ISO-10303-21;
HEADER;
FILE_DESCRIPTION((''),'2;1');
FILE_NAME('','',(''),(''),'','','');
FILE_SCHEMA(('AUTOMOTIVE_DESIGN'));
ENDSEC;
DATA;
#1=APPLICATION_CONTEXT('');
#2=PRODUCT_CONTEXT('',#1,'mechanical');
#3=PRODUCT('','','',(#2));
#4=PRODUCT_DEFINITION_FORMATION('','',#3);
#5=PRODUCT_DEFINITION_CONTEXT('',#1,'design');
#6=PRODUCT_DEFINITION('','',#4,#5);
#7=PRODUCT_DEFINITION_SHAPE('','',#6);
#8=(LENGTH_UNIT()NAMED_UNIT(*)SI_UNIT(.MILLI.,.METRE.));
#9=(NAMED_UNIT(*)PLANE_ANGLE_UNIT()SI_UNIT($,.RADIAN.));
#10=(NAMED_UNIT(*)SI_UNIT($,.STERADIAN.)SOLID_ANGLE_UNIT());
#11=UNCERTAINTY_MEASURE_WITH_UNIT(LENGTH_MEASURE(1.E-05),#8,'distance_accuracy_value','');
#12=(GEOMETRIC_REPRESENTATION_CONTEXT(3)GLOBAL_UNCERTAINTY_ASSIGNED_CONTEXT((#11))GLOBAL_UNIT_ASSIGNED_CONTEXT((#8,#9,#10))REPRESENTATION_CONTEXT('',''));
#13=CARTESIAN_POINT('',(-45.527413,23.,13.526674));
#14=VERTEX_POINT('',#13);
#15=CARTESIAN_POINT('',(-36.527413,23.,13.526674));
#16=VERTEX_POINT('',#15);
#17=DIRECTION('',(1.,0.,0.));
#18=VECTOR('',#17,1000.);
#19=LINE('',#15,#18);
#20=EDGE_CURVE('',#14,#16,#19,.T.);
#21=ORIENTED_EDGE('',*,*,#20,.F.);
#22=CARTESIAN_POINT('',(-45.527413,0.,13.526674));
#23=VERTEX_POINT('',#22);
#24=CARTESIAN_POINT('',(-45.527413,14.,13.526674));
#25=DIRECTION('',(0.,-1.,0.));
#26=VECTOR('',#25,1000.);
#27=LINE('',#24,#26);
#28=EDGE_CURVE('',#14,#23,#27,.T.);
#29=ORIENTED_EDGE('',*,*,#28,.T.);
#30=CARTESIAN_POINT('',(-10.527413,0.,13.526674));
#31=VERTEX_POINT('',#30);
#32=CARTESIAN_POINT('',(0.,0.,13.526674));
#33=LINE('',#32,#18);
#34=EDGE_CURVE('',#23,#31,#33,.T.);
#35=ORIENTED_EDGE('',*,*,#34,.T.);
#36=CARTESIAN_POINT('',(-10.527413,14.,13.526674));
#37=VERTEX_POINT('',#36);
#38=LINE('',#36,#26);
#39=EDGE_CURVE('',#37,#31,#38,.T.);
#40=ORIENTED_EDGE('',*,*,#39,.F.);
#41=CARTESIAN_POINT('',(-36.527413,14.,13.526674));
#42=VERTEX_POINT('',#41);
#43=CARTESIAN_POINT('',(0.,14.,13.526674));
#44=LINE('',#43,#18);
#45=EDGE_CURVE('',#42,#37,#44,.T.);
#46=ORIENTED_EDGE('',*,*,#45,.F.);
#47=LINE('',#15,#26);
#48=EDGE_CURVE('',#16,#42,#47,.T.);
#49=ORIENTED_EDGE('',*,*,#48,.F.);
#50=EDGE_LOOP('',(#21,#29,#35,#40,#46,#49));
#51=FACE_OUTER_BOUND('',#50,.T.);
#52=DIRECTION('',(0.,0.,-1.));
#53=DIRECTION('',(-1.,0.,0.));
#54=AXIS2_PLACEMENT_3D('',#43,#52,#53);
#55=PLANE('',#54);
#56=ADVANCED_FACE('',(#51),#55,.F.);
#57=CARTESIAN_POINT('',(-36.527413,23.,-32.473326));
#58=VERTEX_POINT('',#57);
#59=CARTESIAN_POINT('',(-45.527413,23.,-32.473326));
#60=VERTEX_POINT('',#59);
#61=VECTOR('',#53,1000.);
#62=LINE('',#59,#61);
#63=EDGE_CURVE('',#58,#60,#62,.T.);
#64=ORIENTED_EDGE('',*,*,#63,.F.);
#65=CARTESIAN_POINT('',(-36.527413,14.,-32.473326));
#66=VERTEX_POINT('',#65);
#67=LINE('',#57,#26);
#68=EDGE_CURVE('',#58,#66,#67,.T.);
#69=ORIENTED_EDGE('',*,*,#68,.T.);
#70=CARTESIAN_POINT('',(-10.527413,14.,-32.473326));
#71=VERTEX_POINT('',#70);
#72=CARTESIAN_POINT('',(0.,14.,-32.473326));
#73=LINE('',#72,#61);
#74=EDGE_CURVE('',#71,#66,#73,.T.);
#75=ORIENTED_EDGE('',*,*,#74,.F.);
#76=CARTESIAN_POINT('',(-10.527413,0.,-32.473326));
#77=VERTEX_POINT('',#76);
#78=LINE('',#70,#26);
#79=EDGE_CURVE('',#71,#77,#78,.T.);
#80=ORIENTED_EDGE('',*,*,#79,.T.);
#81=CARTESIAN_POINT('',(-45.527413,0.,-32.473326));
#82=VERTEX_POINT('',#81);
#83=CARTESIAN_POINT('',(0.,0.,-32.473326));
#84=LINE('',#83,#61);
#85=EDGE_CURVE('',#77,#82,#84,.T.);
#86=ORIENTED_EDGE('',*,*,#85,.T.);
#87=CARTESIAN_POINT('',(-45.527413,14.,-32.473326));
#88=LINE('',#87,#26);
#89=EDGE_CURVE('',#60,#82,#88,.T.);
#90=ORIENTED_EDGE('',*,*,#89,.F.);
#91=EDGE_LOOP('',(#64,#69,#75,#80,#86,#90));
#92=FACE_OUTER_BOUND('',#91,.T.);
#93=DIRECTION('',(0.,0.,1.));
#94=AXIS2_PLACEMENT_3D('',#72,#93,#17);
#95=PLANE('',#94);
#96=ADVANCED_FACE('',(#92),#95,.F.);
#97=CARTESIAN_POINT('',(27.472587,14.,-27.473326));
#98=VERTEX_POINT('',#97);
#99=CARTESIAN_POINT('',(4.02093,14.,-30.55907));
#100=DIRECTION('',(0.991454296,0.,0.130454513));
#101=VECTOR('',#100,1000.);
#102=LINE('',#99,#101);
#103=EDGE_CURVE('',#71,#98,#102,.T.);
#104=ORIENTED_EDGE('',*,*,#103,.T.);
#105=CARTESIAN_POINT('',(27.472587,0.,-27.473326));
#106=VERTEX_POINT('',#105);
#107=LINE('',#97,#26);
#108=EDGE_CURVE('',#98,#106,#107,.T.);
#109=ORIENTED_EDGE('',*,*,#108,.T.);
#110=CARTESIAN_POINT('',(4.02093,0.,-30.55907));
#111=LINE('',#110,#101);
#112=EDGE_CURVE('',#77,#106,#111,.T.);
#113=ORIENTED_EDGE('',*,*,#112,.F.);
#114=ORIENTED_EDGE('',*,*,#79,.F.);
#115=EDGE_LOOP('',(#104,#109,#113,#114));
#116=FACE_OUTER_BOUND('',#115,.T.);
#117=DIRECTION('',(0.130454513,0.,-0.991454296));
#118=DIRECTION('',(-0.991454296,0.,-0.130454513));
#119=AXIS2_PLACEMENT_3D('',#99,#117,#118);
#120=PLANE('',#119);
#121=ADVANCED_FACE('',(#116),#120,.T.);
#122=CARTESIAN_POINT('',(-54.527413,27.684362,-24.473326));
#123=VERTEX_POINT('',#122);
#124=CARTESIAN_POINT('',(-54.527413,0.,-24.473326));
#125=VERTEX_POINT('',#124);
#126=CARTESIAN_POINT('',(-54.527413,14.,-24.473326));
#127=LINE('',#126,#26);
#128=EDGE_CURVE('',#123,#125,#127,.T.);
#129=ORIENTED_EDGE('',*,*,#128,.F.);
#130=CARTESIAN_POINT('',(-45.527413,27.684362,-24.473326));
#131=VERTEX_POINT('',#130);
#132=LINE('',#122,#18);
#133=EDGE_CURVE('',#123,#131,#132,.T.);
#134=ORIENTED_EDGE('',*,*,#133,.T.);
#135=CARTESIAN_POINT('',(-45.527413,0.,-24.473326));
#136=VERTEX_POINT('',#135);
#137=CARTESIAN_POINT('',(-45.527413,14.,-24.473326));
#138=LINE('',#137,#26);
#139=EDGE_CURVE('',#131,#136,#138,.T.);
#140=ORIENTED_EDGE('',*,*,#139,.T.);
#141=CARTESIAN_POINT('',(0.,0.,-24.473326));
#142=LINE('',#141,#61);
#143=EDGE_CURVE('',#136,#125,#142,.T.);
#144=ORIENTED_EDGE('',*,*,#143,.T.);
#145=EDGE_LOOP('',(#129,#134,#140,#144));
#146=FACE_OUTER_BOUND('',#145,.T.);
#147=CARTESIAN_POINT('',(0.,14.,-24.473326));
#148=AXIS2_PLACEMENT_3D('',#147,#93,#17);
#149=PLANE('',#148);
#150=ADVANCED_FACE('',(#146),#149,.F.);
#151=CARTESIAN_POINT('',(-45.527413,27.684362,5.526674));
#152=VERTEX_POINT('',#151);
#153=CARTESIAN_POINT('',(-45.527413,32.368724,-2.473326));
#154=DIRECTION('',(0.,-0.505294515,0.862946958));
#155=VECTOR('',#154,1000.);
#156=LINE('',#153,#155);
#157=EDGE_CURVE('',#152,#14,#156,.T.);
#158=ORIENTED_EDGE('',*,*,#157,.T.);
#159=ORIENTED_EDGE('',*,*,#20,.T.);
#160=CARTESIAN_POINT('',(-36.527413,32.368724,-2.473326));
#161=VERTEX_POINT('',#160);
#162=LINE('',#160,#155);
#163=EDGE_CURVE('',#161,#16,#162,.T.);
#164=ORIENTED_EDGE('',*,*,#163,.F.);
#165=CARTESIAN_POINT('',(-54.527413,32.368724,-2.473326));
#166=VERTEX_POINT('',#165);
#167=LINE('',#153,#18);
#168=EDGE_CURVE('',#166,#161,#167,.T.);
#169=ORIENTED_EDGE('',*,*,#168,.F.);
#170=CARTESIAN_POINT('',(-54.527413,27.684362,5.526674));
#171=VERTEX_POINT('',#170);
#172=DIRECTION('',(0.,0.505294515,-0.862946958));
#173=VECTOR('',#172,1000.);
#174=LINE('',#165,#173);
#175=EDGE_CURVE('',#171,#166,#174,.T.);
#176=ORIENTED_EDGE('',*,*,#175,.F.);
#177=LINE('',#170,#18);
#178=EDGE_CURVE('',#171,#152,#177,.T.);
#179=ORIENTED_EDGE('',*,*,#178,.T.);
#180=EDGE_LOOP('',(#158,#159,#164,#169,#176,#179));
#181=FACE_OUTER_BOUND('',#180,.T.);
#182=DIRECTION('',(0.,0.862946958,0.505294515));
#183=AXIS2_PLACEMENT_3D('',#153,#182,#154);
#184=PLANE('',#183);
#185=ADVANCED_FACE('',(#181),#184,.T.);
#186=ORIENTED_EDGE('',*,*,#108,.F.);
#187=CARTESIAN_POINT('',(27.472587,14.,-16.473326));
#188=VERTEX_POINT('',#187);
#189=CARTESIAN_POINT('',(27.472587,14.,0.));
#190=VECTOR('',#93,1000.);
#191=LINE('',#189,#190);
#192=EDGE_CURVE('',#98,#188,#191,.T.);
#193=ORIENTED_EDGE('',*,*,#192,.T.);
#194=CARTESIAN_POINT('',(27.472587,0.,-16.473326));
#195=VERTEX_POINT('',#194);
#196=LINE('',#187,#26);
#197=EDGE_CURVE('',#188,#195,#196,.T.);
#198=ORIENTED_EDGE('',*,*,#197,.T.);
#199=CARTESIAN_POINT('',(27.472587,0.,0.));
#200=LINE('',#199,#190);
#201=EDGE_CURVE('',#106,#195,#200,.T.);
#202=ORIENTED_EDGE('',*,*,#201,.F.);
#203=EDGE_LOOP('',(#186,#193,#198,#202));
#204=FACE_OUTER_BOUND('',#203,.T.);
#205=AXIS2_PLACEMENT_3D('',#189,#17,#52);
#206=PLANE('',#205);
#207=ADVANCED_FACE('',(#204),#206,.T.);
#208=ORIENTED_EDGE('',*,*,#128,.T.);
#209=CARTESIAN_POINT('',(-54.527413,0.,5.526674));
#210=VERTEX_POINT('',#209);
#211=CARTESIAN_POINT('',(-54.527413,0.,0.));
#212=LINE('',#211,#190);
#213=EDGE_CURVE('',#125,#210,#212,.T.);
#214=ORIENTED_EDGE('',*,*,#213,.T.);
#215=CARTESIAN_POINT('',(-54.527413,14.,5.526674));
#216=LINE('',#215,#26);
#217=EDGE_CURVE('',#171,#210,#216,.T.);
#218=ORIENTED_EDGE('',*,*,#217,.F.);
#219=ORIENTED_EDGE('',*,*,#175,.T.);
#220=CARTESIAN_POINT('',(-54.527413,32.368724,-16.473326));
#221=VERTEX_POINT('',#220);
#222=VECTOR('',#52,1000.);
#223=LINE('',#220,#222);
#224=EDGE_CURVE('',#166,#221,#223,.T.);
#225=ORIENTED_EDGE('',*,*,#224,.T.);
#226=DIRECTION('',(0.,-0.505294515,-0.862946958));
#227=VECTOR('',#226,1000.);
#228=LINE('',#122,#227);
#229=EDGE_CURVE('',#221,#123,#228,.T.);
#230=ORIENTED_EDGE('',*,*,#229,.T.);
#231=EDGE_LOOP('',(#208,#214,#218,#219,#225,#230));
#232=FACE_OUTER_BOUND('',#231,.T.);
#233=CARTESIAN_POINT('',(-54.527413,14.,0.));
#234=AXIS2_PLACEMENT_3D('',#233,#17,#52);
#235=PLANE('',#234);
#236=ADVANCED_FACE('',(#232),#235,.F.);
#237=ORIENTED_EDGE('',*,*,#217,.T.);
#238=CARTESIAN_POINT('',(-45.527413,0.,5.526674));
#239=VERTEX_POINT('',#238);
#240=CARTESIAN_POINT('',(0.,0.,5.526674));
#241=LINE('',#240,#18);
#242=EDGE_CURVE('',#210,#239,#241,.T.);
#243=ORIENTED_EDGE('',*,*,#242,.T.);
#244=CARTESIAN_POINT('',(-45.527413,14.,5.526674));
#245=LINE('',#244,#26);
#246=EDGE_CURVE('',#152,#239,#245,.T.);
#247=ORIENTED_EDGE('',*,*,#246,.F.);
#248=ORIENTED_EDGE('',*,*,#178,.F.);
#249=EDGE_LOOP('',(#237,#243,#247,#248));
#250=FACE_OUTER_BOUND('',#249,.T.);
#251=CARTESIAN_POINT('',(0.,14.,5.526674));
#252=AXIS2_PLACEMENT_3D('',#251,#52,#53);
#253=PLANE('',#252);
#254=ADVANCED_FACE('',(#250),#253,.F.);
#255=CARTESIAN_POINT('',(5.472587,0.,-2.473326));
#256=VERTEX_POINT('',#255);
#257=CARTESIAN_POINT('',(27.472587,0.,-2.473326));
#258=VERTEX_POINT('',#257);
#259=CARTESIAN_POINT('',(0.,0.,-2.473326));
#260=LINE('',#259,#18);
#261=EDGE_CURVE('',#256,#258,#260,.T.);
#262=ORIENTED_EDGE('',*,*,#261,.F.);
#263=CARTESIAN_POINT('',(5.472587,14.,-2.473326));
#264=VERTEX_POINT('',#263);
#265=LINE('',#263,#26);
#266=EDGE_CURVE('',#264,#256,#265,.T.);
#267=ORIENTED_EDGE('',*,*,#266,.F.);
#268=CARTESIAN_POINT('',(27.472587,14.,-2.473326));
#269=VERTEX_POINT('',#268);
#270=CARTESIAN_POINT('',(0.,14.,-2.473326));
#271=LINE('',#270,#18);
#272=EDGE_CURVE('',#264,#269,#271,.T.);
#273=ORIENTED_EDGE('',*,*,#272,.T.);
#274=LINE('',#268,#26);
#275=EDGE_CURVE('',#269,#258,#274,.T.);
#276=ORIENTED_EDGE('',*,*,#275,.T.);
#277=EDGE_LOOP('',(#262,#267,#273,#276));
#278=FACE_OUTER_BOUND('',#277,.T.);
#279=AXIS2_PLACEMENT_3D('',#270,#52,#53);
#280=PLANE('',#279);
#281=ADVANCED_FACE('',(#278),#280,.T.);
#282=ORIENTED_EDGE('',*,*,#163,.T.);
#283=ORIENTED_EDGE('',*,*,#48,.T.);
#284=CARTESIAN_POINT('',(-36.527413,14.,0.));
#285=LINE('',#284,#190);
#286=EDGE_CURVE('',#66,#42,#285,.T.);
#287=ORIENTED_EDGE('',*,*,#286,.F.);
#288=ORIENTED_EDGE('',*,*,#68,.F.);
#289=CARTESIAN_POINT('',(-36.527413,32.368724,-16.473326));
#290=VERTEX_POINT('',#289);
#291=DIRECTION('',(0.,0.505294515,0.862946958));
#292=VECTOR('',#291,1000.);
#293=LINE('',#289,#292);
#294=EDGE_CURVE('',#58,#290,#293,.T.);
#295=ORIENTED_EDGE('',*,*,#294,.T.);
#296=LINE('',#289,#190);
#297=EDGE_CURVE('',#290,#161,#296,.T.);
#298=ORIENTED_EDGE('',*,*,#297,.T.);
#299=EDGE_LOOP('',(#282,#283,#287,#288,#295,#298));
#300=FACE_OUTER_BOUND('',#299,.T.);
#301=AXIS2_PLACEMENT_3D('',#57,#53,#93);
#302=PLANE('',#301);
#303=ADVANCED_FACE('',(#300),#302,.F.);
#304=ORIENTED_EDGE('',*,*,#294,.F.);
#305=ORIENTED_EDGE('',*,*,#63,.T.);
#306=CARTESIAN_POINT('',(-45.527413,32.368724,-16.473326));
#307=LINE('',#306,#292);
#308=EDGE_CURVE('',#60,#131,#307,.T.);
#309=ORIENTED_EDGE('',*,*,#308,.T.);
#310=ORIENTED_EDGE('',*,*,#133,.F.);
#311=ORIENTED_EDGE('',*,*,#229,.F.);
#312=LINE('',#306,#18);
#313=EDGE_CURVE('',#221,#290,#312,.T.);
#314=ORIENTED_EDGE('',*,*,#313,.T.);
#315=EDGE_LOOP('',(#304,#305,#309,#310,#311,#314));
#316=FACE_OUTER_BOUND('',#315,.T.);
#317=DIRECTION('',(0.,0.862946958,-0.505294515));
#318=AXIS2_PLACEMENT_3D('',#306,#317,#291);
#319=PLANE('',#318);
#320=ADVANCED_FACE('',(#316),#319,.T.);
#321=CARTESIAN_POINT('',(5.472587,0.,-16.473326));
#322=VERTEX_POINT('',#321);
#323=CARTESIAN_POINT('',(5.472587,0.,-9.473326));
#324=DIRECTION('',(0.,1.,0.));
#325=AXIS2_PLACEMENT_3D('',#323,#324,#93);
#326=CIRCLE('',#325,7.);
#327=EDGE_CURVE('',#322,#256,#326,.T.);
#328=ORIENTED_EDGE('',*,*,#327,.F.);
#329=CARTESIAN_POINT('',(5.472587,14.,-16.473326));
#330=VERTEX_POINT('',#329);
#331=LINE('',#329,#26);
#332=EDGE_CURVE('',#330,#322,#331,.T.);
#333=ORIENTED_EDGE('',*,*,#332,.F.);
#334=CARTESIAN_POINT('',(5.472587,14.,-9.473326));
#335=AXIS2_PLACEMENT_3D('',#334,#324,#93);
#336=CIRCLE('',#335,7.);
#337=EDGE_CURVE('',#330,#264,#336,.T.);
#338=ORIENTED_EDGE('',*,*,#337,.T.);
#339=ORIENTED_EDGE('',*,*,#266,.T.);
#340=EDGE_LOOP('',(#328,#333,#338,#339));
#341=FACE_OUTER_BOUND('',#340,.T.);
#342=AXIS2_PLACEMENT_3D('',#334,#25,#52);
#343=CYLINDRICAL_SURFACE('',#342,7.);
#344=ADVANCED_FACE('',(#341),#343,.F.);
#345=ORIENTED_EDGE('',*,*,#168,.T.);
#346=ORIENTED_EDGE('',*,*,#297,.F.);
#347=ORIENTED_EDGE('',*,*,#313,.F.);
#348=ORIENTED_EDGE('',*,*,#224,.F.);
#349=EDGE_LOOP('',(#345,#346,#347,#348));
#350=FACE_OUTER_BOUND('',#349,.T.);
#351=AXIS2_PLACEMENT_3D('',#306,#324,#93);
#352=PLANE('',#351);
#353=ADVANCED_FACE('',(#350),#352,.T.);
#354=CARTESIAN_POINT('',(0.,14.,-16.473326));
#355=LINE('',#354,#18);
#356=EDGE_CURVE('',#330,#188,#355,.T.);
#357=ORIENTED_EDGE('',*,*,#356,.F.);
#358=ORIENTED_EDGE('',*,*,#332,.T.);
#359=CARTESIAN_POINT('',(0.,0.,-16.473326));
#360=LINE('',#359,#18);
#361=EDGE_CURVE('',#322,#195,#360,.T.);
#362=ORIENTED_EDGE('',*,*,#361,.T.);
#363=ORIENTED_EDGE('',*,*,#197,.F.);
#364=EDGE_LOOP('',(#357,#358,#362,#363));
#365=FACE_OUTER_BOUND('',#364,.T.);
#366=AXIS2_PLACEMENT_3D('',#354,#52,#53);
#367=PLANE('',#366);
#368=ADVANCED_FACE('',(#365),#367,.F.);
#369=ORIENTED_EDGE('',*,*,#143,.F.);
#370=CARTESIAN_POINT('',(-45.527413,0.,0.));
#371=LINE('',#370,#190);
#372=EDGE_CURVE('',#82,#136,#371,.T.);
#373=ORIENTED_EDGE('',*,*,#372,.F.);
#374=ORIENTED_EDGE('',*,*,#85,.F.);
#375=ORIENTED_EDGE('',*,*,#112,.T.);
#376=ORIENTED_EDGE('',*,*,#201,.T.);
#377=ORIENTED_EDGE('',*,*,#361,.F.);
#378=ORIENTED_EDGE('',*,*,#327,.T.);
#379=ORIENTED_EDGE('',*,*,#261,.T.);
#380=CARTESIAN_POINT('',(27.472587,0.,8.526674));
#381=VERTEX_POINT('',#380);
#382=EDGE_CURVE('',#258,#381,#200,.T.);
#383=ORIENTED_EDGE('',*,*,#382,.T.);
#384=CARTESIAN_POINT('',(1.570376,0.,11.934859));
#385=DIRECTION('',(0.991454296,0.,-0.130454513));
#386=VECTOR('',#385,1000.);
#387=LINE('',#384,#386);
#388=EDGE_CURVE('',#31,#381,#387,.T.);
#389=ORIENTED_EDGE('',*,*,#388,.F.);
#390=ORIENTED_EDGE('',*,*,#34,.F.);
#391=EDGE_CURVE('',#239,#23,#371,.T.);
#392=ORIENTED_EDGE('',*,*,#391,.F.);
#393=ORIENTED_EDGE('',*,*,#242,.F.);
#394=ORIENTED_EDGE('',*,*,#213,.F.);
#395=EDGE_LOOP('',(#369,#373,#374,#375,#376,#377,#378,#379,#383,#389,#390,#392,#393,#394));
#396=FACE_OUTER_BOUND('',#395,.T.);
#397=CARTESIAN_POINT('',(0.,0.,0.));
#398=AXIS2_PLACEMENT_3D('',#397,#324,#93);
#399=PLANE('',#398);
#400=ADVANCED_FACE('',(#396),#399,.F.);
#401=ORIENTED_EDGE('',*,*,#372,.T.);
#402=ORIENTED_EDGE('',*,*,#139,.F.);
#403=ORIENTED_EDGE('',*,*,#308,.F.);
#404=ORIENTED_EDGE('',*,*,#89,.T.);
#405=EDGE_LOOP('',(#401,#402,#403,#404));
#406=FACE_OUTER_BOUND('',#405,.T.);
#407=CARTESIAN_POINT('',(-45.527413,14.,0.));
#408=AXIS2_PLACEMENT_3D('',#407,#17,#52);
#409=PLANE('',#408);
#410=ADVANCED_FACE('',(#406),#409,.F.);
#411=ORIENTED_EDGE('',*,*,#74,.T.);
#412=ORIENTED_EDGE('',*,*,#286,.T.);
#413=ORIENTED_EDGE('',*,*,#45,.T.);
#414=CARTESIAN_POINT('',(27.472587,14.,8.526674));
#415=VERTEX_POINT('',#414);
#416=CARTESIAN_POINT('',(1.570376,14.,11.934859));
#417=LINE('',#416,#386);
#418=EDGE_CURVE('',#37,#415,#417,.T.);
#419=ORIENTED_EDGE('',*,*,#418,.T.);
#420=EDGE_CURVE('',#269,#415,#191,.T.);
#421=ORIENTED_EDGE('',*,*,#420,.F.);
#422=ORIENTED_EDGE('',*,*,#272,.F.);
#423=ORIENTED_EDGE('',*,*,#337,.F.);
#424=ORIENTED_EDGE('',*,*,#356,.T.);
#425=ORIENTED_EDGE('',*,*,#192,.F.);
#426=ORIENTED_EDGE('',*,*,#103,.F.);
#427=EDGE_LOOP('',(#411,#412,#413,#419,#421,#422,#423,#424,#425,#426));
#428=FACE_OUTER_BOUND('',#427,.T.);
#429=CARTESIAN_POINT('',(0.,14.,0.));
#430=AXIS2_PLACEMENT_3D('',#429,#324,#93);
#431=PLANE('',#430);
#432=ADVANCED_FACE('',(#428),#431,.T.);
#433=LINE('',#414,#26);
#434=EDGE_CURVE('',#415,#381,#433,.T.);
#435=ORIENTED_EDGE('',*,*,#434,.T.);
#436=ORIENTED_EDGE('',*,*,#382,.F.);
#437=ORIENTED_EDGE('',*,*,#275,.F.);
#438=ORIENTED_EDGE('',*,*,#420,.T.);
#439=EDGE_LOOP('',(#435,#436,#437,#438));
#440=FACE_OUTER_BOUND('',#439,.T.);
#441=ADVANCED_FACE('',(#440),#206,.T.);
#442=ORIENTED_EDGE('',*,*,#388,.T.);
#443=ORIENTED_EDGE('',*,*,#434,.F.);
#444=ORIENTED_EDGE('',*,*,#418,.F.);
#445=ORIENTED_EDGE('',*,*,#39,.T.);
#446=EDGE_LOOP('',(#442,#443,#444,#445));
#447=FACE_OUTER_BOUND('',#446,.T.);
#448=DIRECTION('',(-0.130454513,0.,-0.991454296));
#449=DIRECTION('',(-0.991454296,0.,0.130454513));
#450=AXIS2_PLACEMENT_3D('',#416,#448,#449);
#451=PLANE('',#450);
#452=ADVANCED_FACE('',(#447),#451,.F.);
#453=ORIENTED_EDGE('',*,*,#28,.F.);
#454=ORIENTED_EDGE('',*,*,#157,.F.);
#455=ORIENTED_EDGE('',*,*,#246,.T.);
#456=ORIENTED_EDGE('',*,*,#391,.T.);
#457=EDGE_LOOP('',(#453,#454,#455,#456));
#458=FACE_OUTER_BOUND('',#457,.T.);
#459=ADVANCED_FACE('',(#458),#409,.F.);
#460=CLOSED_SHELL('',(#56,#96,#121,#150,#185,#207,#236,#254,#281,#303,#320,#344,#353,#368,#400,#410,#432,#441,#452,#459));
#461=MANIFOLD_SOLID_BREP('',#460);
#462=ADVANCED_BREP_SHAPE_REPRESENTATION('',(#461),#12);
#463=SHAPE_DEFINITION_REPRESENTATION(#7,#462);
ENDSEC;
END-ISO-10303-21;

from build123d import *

# Parameters (mm, degrees)
SLOTTED_BASE_PLATE_DEPTH = 14
REAR_UPRIGHT_BLOCK_DEPTH = 23
UPPER_STEP_BLOCK_DEPTH   = 9
TOP_BLOCK_DEPTH          = 9


with BuildPart() as part:
    # Slotted Base Plate Sketch → Slotted Base Plate (new body)
    with BuildSketch(Plane(origin=(0, 0, 0), x_dir=(1, 0, 0), z_dir=(0, 1, 0))):
        Polygon((-45.527413465, -5.526673775), (-45.527413465, -13.526673775), (-36.527413465, -13.526673775), (-36.527413465, 32.473326225), (-45.527413465, 32.473326225), (-45.527413465, 24.473326225), (-54.527413465, 24.473326225), (-54.527413465, -5.526673775), align=None)
        with BuildLine():
            ThreePointArc((5.472586535, 16.473326225), (-1.527413465, 9.473326225), (5.472586535, 2.473326225))
            Line((5.472586535, 2.473326225), (27.472586535, 2.473326225))
            Line((27.472586535, 2.473326225), (27.472586535, -8.526673775))
            Line((27.472586535, -8.526673775), (-10.527413465, -13.526673775))
            Line((-10.527413465, -13.526673775), (-36.527413465, -13.526673775))
            Line((-36.527413465, -13.526673775), (-36.527413465, 32.473326225))
            Line((-36.527413465, 32.473326225), (-10.527413465, 32.473326225))
            Line((-10.527413465, 32.473326225), (27.472586535, 27.473326225))
            Line((27.472586535, 27.473326225), (27.472586535, 16.473326225))
            Line((27.472586535, 16.473326225), (5.472586535, 16.473326225))
        make_face()
    extrude(amount=SLOTTED_BASE_PLATE_DEPTH)

    # Rear Upright Block Sketch → Rear Upright Block (add)
    with BuildSketch(Plane(origin=(0, 0, 0), x_dir=(1, 0, 0), z_dir=(0, 1, 0))):
        Polygon((-45.527413465, 32.473326225), (-36.527413465, 32.473326225), (-36.527413465, -13.526673775), (-45.527413465, -13.526673775), (-45.527413465, -5.526673775), (-54.527413465, -5.526673775), (-54.527413465, 24.473326225), (-45.527413465, 24.473326225), align=None)
    extrude(amount=REAR_UPRIGHT_BLOCK_DEPTH)

    # Upper Step Sketch → Upper Step Block (add)
    with BuildSketch(Plane(origin=(-36.527413465, 0, 0), x_dir=(0, 0, -1), z_dir=(1, 0, 0))):
        Polygon((-13.526673775, 23), (32.473326225, 23), (16.473326225, 32.368724422), (2.473326225, 32.368724422), align=None)
    extrude(amount=-UPPER_STEP_BLOCK_DEPTH)

    # Top Block Sketch → Top Block (add)
    with BuildSketch(Plane.ZY.offset(45.527413465)):
        Polygon((-24.473326225, 23), (-24.473326225, 27.684362211), (-16.473326225, 32.368724422), (-2.473326225, 32.368724422), (5.526673775, 27.684362211), (5.526673775, 23), align=None)
    extrude(amount=TOP_BLOCK_DEPTH)


solid = part.part
